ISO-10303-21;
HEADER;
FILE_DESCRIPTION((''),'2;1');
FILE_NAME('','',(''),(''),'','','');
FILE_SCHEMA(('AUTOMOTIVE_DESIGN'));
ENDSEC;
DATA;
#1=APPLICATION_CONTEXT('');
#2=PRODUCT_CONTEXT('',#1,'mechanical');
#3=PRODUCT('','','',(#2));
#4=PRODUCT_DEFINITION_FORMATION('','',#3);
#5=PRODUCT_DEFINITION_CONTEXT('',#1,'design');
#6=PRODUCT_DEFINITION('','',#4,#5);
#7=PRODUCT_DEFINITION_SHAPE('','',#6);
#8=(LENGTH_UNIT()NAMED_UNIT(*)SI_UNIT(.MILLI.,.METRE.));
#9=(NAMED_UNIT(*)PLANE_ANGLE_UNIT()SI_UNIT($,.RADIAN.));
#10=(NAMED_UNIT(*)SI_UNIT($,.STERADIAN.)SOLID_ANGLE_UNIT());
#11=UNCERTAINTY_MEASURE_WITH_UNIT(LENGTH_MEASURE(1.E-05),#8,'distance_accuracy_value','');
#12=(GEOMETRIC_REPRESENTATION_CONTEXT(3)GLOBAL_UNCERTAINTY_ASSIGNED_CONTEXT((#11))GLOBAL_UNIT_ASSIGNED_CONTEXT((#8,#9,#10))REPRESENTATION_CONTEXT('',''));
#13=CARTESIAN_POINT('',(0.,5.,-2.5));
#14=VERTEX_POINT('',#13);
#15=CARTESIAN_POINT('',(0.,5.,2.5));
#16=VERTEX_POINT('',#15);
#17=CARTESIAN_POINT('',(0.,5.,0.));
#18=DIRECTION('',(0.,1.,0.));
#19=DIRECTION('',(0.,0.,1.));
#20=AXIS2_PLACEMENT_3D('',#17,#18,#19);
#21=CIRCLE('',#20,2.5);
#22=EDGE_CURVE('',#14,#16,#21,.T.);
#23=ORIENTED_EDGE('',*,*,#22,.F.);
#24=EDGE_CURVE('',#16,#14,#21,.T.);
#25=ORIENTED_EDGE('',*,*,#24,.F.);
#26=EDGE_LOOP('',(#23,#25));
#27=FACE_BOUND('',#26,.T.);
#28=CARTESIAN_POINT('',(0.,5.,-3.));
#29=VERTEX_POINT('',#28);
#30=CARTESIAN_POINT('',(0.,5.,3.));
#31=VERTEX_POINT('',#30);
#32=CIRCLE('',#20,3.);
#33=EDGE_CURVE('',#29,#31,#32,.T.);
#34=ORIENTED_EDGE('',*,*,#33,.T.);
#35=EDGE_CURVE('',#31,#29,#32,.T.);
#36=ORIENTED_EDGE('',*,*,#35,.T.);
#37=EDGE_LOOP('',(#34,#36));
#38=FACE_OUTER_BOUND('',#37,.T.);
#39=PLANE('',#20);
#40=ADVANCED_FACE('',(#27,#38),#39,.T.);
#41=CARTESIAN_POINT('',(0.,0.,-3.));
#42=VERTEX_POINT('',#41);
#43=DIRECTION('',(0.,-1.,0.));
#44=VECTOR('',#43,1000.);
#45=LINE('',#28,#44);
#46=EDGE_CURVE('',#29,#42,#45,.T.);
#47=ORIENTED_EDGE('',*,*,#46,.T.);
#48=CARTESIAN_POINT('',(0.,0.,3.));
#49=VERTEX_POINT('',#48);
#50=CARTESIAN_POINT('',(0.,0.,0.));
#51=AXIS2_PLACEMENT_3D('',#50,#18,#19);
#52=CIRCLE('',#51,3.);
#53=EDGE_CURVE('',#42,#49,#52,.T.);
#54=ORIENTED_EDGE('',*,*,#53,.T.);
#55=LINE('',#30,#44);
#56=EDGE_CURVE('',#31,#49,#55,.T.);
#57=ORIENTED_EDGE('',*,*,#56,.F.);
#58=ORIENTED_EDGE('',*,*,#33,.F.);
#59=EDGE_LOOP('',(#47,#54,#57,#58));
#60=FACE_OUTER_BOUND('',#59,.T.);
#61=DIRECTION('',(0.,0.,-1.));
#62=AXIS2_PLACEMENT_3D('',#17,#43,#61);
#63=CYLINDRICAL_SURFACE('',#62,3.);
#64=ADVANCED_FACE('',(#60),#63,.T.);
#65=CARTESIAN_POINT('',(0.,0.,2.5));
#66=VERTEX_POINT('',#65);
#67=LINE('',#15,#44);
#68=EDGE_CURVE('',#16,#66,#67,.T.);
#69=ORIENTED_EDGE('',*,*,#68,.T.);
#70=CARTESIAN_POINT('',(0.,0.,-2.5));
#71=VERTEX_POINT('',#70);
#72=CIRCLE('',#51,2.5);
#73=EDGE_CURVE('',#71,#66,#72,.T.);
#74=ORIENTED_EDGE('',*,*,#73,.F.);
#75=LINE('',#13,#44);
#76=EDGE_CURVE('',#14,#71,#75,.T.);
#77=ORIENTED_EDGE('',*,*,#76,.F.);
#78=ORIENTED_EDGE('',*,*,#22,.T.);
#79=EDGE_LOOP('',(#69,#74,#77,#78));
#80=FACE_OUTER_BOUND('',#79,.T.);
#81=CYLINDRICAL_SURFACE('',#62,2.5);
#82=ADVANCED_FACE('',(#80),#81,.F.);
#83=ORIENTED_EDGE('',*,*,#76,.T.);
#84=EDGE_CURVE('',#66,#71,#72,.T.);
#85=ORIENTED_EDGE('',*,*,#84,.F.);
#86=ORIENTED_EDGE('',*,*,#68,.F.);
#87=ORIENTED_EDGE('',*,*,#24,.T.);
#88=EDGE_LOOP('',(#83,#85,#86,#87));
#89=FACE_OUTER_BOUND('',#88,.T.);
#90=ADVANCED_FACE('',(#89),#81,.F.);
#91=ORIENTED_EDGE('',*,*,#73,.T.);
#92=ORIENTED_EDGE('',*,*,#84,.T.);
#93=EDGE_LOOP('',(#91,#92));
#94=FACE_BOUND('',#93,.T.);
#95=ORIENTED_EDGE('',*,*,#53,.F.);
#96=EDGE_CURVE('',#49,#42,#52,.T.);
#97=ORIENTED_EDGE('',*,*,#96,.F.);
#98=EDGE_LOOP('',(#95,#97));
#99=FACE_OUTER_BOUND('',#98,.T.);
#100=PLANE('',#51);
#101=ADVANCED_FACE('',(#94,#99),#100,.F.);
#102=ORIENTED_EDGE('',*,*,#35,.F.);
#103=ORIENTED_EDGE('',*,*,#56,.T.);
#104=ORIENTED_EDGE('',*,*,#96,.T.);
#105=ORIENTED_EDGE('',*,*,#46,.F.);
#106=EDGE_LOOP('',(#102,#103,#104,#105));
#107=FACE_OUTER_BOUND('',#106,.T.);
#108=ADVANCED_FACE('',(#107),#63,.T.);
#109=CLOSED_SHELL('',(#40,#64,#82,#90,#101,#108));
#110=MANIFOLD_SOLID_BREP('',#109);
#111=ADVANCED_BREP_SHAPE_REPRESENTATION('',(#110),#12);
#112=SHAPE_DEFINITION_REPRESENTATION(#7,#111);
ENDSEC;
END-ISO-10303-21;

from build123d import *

# Parameters (mm, degrees)
SKETCH1_R           = 3
SKETCH1_R_2         = 2.5
BOSS_EXTRUDE1_DEPTH = 5


with BuildPart() as part:
    # Sketch1 → Boss-Extrude1 (new body)
    with BuildSketch(Plane(origin=(0, 0, 0), x_dir=(1, 0, 0), z_dir=(0, 1, 0))):
        with Locations(Location((0, 0, 0), (0, 0, 270))):
            Circle(SKETCH1_R)
        with Locations(Location((0, 0, 0), (0, 0, 270))):
            Circle(SKETCH1_R_2, mode=Mode.SUBTRACT)
    extrude(amount=BOSS_EXTRUDE1_DEPTH)


solid = part.part
